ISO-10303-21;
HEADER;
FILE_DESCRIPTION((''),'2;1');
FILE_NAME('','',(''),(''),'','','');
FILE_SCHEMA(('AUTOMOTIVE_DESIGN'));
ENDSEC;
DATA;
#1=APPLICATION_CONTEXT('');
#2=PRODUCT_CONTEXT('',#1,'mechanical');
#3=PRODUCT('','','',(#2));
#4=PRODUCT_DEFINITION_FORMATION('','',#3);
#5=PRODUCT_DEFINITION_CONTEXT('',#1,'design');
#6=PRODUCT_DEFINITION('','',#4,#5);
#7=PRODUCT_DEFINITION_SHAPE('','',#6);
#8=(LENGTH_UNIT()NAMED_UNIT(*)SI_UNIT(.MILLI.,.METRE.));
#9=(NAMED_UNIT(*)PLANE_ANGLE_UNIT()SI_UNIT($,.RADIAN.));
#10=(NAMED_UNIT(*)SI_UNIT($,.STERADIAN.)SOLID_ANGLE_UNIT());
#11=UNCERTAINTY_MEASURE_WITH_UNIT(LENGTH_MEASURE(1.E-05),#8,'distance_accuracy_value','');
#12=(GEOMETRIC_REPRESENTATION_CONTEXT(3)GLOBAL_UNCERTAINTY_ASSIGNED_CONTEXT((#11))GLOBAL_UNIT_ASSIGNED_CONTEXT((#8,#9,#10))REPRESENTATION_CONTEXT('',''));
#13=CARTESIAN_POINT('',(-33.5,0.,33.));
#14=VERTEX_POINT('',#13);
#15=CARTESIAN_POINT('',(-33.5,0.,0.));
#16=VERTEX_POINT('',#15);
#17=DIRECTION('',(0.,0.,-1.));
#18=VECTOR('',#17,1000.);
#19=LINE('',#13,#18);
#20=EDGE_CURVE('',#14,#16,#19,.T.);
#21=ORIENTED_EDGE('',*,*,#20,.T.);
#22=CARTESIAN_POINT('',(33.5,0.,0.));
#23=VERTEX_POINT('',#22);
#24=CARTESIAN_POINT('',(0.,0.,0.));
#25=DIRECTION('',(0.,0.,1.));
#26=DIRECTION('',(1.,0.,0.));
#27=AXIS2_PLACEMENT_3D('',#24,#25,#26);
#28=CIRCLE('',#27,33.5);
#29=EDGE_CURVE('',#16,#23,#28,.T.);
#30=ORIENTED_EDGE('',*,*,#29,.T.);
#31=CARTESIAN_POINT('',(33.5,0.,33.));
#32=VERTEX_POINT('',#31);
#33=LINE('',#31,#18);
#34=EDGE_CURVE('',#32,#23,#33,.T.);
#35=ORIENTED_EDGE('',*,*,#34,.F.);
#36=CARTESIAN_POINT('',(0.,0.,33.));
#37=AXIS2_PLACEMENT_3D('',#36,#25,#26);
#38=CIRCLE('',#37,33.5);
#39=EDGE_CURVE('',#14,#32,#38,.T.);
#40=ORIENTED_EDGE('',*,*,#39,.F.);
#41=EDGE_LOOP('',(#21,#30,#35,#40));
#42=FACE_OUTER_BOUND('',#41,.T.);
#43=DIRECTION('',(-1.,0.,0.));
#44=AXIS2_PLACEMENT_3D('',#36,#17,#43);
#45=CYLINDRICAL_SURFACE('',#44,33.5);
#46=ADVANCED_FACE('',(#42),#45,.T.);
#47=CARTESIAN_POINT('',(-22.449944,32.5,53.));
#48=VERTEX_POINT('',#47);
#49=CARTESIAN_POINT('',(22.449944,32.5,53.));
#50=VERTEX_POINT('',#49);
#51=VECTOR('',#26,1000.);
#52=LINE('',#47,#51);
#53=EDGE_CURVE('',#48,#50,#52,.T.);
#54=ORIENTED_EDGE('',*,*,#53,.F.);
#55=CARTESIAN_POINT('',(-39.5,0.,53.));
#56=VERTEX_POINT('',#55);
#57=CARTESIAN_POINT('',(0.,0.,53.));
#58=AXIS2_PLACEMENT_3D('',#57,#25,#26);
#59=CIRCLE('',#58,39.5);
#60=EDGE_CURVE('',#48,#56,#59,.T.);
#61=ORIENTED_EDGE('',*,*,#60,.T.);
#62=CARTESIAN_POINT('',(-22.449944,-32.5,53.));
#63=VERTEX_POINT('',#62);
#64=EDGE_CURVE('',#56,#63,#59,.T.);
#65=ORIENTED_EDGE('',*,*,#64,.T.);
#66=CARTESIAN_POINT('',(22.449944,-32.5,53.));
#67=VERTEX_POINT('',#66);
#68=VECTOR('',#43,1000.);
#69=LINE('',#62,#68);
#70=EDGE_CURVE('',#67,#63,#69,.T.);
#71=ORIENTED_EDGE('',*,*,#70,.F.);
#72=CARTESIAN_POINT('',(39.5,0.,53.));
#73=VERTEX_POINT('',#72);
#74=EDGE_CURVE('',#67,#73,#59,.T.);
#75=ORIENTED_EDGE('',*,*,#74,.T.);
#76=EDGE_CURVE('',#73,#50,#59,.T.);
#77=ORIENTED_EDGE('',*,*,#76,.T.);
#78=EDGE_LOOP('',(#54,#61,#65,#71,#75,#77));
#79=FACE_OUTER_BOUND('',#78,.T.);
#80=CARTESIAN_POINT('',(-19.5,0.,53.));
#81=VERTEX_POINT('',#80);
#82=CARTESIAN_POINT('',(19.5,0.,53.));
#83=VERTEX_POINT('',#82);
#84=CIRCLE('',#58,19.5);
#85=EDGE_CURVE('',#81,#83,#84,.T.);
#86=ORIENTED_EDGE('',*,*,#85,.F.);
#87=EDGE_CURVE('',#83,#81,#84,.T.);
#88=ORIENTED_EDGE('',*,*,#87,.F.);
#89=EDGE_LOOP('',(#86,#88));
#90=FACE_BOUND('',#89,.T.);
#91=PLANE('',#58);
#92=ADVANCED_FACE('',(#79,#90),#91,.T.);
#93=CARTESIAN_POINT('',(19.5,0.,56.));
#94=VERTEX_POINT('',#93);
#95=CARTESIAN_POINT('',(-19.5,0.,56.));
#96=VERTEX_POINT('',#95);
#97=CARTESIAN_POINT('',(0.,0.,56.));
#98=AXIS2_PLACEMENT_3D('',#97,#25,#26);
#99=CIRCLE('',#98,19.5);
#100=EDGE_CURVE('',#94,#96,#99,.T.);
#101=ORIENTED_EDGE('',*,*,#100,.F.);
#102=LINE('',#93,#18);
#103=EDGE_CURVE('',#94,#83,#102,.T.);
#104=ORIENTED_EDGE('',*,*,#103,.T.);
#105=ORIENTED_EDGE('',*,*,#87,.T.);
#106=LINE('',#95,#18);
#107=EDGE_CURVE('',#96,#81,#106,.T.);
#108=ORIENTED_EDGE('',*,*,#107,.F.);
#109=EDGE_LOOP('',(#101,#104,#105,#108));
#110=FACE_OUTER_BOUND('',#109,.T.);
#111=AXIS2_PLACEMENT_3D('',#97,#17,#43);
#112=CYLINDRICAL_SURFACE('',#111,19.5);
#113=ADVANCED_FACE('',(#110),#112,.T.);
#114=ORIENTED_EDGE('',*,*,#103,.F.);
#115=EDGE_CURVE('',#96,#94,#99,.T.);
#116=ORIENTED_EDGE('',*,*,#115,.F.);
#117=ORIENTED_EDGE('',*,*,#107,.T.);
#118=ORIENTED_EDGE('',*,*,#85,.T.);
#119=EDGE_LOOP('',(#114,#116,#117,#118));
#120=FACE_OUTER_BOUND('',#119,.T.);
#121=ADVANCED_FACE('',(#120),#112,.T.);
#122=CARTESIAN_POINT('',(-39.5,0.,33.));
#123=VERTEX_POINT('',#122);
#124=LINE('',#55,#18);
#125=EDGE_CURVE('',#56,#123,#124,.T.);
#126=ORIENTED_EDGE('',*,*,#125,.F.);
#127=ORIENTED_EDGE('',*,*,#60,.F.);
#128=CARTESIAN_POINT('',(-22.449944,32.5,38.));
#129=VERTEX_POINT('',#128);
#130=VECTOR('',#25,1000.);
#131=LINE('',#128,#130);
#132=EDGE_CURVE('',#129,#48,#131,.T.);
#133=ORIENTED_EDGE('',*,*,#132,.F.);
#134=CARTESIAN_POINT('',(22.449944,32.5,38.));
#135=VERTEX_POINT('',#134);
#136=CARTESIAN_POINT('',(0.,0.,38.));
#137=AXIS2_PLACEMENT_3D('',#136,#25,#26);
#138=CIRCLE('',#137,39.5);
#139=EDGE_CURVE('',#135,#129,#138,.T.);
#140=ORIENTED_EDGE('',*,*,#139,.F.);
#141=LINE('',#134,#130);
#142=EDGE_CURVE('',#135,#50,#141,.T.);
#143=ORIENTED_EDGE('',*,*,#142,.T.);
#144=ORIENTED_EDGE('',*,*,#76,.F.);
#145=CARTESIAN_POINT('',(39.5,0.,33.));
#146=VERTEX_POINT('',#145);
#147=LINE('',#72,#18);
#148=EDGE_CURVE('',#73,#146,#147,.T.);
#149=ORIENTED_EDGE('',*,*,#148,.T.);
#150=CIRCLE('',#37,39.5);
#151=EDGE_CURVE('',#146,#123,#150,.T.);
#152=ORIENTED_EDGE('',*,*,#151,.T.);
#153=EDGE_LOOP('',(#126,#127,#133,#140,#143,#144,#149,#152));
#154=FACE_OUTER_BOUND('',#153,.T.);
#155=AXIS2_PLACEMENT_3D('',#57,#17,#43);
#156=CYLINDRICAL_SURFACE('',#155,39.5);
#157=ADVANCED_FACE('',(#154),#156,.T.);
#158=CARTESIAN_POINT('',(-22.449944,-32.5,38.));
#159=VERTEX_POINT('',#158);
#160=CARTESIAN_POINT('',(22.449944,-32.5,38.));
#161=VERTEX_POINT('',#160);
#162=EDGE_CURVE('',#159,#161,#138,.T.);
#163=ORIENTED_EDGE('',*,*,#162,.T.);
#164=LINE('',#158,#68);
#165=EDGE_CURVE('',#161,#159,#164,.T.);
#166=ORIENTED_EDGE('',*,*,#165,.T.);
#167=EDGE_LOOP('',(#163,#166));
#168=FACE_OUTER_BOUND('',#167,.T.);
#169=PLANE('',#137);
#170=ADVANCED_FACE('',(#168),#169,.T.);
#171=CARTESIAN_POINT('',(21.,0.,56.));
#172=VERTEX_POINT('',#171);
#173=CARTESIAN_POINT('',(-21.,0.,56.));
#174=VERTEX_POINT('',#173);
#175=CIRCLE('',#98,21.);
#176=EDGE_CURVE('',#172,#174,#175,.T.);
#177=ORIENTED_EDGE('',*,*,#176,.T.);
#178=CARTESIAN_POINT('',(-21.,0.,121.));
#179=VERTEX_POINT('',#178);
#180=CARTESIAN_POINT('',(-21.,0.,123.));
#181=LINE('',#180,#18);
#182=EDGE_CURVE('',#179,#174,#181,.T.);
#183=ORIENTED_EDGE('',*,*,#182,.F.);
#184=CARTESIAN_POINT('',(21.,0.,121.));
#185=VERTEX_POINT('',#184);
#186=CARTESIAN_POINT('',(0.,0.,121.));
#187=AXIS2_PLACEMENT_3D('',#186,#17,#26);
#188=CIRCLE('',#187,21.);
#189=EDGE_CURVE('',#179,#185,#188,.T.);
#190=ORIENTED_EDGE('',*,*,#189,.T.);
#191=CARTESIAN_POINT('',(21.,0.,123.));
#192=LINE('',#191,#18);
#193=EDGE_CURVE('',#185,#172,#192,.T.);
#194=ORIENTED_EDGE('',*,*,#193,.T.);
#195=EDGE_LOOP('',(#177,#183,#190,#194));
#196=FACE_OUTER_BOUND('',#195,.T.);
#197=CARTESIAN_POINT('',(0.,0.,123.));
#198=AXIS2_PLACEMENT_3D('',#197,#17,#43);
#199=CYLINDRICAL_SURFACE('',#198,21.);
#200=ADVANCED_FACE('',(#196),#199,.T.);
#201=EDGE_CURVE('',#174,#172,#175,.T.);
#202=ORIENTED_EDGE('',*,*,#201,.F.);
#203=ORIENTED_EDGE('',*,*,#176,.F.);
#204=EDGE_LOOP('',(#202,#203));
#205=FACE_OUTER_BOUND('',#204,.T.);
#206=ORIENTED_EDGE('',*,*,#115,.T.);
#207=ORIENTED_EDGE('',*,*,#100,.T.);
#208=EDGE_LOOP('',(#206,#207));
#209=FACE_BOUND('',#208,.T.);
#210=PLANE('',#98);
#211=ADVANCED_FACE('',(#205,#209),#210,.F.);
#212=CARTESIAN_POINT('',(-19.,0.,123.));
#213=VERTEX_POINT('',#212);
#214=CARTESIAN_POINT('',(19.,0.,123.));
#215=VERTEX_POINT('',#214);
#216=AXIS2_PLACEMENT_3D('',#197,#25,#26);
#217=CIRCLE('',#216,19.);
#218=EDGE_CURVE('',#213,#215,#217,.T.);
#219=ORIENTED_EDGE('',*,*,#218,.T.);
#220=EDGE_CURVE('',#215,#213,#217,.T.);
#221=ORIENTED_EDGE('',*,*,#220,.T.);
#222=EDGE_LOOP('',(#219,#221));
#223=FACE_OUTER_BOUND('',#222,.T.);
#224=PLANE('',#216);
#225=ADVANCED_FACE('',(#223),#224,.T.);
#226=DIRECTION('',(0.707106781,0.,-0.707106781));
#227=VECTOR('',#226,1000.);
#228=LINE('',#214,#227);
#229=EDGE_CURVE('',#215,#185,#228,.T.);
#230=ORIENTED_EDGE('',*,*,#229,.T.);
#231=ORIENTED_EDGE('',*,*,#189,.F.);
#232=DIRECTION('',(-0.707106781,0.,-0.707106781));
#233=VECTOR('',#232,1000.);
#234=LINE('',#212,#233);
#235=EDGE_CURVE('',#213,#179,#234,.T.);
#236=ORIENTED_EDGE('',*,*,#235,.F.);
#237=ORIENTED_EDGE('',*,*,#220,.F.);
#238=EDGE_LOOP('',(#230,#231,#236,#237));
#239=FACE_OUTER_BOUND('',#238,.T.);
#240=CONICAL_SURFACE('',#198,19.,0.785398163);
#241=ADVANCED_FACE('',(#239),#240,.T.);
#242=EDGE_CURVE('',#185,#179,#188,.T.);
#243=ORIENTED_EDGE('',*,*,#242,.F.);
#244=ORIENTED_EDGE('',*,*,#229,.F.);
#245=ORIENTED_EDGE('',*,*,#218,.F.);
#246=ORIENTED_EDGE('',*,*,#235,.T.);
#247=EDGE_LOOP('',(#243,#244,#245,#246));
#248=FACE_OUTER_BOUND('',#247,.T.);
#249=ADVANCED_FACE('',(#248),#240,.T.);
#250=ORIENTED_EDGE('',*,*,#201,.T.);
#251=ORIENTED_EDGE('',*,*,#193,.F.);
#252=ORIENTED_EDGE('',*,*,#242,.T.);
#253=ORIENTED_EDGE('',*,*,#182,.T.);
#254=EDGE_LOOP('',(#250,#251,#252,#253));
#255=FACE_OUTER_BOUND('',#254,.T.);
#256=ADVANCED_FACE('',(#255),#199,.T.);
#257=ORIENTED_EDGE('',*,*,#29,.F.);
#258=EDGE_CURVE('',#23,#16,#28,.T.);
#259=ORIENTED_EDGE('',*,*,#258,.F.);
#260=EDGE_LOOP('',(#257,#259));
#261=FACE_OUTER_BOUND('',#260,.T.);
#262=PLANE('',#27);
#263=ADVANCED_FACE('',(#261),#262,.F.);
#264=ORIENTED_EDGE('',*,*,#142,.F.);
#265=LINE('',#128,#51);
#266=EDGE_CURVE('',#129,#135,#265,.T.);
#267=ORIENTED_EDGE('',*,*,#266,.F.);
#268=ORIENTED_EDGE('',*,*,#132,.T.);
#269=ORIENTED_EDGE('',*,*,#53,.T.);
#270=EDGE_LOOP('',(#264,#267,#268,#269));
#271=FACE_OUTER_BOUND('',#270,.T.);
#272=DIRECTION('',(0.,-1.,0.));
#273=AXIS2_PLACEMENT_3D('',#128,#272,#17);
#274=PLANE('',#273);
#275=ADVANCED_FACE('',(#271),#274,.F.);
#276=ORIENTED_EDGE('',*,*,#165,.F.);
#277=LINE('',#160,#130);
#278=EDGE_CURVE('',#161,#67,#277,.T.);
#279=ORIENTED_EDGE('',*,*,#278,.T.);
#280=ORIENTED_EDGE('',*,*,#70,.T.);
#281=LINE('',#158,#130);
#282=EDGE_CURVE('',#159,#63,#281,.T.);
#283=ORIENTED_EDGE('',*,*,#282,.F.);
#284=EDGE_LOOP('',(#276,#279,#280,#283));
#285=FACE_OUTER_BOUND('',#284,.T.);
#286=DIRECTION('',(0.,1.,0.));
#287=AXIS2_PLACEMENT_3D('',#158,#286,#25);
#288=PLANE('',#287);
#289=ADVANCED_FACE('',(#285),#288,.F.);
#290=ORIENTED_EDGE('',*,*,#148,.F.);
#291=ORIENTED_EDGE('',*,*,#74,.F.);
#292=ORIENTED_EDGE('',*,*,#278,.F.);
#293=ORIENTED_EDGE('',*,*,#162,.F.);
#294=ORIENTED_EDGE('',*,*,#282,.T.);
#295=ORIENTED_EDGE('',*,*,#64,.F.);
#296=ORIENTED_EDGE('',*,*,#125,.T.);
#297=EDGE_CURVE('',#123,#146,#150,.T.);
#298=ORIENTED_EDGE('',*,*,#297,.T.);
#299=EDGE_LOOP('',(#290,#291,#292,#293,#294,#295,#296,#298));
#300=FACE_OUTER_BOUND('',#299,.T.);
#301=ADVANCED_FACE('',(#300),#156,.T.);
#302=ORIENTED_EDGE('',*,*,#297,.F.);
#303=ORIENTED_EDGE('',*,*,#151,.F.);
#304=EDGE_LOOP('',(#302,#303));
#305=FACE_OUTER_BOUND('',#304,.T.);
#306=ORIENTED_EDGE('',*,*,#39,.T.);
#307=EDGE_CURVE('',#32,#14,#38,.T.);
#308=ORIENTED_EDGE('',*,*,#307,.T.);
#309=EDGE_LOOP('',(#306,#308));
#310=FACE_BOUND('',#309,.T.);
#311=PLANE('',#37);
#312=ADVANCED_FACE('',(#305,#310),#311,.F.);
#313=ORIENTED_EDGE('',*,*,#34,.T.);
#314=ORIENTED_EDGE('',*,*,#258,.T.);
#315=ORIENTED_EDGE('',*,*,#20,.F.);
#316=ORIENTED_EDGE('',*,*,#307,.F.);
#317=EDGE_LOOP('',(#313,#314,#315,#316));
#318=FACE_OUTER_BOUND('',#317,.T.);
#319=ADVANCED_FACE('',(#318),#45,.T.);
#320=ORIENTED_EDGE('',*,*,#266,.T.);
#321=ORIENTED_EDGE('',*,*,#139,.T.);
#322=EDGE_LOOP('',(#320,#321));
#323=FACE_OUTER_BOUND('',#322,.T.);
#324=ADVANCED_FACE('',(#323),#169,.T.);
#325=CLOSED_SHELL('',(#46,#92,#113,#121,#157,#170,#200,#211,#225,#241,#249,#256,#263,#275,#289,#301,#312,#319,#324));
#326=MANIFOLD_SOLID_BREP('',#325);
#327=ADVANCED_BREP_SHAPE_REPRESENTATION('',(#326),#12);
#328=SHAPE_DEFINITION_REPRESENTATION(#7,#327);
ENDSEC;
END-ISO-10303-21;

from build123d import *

# Parameters (mm, degrees)
SKETCH1_R           = 33.5
BOSS_EXTRUDE1_DEPTH = 33
SKETCH2_R           = 39.5
BOSS_EXTRUDE2_DEPTH = 20
CUT_EXTRUDE1_START  = -15
CUT_EXTRUDE1_DEPTH  = 15
SKETCH4_R           = 19.5
BOSS_EXTRUDE3_DEPTH = 3
SKETCH5_R           = 21
BOSS_EXTRUDE4_DEPTH = 67
CHAMFER1_SIZE       = 2


with BuildPart() as part:
    # Sketch1 → Boss-Extrude1 (new body)
    with BuildSketch(Plane.XY):
        Circle(SKETCH1_R)
    extrude(amount=BOSS_EXTRUDE1_DEPTH)

    # Sketch2 → Boss-Extrude2 (add)
    with BuildSketch(Plane.XY.offset(33)):
        Circle(SKETCH2_R)
    extrude(amount=BOSS_EXTRUDE2_DEPTH)

    # Sketch3 → Cut-Extrude1 (cut)
    with BuildSketch(Plane.XY.offset(53).offset(CUT_EXTRUDE1_START)):
        with BuildLine():
            Line((-22.449944321, 32.5), (22.449944321, 32.5))
            ThreePointArc((22.449944321, 32.5), (0, 39.5), (-22.449944321, 32.5))
        make_face()
        with BuildLine():
            Line((-22.449944321, -32.5), (22.449944321, -32.5))
            ThreePointArc((22.449944321, -32.5), (0, -39.5), (-22.449944321, -32.5))
        make_face()
    extrude(amount=CUT_EXTRUDE1_DEPTH, mode=Mode.SUBTRACT)

    # Sketch4 → Boss-Extrude3 (add)
    with BuildSketch(Plane.XY.offset(53)):
        Circle(SKETCH4_R)
    extrude(amount=BOSS_EXTRUDE3_DEPTH)

    # Sketch5 → Boss-Extrude4 (add)
    with BuildSketch(Plane.XY.offset(56)):
        Circle(SKETCH5_R)
    extrude(amount=BOSS_EXTRUDE4_DEPTH)

    # Chamfer1
    chamfer1_edges = [part.edges().sort_by_distance(p)[0] for p in [
        (-21, 0, 123),
    ]]
    chamfer(chamfer1_edges, length=CHAMFER1_SIZE)


solid = part.part
